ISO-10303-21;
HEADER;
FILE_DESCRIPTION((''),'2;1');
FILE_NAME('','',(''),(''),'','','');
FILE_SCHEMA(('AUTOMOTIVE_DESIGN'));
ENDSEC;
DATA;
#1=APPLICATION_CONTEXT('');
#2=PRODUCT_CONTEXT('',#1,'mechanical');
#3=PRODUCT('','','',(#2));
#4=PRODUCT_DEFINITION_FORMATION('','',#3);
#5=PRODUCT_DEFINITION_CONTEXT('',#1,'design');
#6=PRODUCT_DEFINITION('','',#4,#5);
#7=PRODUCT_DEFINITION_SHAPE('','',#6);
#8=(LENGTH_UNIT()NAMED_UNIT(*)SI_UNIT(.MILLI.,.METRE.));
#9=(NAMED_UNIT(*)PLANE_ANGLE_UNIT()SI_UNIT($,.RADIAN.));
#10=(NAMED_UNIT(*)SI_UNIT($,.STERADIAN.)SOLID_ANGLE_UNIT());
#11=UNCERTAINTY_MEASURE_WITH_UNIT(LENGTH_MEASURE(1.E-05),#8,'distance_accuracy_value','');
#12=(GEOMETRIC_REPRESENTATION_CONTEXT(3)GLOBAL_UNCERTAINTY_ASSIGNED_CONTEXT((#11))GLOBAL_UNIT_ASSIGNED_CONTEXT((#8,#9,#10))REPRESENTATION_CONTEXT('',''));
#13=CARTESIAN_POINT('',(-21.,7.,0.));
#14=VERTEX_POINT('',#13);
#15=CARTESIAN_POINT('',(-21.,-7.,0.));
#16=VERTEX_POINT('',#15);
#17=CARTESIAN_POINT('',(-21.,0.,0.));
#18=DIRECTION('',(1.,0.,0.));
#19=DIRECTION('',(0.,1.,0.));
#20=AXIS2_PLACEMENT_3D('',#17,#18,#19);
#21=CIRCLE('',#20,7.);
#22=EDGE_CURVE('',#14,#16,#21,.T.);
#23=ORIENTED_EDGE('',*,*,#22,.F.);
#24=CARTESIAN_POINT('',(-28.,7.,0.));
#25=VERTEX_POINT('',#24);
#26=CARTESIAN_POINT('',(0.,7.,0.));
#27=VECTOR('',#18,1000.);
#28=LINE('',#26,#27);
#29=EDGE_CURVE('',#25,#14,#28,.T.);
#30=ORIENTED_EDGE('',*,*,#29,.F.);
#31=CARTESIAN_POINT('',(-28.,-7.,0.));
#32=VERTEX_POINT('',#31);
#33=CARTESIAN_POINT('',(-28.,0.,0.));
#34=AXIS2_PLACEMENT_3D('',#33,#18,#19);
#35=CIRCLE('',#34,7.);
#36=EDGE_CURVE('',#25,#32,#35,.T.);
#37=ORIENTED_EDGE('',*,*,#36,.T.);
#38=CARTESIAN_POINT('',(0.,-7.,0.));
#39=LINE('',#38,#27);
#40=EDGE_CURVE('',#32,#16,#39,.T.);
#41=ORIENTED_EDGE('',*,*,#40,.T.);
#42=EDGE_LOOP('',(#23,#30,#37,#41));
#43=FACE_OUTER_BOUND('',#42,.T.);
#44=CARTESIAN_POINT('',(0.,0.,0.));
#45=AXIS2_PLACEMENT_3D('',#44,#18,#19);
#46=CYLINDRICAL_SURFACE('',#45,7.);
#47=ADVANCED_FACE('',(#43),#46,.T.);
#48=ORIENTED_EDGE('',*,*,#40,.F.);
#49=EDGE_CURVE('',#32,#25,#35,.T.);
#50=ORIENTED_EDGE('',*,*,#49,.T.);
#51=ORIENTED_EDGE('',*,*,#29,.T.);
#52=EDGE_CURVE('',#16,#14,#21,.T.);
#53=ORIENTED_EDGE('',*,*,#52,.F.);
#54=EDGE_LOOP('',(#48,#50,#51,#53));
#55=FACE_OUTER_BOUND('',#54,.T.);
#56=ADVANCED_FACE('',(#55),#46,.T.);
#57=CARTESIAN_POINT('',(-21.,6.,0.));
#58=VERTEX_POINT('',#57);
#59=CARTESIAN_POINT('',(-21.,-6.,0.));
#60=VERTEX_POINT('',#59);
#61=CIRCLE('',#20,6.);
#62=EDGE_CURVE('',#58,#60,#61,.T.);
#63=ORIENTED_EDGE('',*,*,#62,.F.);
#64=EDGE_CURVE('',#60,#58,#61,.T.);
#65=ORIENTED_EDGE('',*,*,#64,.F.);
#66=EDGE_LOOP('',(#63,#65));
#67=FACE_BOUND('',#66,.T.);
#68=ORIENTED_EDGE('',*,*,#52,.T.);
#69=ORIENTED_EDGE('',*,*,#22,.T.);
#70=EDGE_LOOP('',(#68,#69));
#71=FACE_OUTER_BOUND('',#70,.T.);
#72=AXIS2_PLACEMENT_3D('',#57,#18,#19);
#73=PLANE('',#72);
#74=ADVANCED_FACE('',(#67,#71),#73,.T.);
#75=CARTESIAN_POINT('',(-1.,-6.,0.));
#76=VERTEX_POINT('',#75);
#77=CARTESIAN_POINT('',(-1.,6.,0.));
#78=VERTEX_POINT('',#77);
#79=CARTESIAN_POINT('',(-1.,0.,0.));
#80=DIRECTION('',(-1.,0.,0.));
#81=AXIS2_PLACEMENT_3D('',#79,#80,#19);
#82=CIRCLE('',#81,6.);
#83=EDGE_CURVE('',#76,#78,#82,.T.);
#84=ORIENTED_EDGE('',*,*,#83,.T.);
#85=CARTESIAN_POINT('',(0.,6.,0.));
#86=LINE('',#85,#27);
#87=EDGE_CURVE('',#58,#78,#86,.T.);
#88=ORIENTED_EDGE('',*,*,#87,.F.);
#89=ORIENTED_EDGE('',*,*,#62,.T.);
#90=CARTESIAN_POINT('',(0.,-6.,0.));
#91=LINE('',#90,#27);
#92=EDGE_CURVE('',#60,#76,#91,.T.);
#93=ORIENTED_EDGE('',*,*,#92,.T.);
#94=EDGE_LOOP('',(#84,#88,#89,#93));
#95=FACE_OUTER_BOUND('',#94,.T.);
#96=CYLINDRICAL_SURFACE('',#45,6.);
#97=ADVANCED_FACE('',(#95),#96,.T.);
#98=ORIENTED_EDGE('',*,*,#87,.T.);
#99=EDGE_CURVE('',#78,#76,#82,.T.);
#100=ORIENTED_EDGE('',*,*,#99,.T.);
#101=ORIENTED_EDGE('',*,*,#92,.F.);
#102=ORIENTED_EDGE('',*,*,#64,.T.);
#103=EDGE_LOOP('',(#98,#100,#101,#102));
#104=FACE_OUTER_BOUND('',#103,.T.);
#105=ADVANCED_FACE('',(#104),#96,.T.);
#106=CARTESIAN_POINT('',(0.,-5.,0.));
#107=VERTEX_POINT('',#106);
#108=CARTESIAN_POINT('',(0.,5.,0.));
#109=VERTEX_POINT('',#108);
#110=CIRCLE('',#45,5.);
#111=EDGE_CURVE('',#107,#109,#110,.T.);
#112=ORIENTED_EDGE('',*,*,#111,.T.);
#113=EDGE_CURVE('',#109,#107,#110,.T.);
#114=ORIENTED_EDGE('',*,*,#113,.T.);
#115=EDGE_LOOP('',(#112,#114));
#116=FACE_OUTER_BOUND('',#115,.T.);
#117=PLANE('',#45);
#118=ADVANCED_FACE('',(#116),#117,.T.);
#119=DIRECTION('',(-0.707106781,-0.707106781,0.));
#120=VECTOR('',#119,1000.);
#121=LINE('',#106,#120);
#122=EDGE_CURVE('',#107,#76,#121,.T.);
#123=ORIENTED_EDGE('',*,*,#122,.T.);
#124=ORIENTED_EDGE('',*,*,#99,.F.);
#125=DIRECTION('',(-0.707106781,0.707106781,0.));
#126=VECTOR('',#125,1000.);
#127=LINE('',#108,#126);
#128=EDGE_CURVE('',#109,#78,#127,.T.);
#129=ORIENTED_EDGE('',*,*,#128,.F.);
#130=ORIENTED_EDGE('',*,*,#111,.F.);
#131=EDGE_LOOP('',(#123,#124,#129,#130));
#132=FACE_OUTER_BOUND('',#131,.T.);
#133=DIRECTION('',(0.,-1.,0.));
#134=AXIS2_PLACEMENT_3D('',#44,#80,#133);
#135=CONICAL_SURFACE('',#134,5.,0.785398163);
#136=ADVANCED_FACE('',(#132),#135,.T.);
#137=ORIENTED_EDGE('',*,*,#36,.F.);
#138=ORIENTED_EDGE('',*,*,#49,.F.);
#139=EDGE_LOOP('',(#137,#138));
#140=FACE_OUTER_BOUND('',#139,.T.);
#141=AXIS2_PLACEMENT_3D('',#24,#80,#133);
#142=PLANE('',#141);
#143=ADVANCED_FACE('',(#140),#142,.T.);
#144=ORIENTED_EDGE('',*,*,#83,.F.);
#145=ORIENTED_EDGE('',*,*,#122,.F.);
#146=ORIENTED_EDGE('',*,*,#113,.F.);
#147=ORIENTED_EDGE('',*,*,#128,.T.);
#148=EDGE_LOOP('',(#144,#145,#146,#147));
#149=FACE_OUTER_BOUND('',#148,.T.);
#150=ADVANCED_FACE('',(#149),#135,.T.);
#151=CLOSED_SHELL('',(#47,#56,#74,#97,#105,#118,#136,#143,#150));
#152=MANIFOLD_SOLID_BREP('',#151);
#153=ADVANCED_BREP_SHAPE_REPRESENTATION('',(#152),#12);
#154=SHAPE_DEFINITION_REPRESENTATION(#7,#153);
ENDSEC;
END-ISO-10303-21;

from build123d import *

# Parameters (mm, degrees)
SHANK_END_CHAMFER_1X45_SIZE = 1


with BuildPart() as part:
    # Bolt Profile Sketch → Bolt Body Revolve (revolve)
    with BuildSketch(Plane.XY):
        Polygon((0, 0), (0, 6), (-21, 6), (-21, 7), (-28, 7), (-28, 0), align=None)
    revolve(axis=Axis((0, 0, 0), (-1, 0, 0)))

    # Shank End Chamfer 1x45
    shank_end_chamfer_1x45_edges = [part.edges().sort_by_distance(p)[0] for p in [
        (0, -6, 0),
    ]]
    chamfer(shank_end_chamfer_1x45_edges, length=SHANK_END_CHAMFER_1X45_SIZE)


solid = part.part
